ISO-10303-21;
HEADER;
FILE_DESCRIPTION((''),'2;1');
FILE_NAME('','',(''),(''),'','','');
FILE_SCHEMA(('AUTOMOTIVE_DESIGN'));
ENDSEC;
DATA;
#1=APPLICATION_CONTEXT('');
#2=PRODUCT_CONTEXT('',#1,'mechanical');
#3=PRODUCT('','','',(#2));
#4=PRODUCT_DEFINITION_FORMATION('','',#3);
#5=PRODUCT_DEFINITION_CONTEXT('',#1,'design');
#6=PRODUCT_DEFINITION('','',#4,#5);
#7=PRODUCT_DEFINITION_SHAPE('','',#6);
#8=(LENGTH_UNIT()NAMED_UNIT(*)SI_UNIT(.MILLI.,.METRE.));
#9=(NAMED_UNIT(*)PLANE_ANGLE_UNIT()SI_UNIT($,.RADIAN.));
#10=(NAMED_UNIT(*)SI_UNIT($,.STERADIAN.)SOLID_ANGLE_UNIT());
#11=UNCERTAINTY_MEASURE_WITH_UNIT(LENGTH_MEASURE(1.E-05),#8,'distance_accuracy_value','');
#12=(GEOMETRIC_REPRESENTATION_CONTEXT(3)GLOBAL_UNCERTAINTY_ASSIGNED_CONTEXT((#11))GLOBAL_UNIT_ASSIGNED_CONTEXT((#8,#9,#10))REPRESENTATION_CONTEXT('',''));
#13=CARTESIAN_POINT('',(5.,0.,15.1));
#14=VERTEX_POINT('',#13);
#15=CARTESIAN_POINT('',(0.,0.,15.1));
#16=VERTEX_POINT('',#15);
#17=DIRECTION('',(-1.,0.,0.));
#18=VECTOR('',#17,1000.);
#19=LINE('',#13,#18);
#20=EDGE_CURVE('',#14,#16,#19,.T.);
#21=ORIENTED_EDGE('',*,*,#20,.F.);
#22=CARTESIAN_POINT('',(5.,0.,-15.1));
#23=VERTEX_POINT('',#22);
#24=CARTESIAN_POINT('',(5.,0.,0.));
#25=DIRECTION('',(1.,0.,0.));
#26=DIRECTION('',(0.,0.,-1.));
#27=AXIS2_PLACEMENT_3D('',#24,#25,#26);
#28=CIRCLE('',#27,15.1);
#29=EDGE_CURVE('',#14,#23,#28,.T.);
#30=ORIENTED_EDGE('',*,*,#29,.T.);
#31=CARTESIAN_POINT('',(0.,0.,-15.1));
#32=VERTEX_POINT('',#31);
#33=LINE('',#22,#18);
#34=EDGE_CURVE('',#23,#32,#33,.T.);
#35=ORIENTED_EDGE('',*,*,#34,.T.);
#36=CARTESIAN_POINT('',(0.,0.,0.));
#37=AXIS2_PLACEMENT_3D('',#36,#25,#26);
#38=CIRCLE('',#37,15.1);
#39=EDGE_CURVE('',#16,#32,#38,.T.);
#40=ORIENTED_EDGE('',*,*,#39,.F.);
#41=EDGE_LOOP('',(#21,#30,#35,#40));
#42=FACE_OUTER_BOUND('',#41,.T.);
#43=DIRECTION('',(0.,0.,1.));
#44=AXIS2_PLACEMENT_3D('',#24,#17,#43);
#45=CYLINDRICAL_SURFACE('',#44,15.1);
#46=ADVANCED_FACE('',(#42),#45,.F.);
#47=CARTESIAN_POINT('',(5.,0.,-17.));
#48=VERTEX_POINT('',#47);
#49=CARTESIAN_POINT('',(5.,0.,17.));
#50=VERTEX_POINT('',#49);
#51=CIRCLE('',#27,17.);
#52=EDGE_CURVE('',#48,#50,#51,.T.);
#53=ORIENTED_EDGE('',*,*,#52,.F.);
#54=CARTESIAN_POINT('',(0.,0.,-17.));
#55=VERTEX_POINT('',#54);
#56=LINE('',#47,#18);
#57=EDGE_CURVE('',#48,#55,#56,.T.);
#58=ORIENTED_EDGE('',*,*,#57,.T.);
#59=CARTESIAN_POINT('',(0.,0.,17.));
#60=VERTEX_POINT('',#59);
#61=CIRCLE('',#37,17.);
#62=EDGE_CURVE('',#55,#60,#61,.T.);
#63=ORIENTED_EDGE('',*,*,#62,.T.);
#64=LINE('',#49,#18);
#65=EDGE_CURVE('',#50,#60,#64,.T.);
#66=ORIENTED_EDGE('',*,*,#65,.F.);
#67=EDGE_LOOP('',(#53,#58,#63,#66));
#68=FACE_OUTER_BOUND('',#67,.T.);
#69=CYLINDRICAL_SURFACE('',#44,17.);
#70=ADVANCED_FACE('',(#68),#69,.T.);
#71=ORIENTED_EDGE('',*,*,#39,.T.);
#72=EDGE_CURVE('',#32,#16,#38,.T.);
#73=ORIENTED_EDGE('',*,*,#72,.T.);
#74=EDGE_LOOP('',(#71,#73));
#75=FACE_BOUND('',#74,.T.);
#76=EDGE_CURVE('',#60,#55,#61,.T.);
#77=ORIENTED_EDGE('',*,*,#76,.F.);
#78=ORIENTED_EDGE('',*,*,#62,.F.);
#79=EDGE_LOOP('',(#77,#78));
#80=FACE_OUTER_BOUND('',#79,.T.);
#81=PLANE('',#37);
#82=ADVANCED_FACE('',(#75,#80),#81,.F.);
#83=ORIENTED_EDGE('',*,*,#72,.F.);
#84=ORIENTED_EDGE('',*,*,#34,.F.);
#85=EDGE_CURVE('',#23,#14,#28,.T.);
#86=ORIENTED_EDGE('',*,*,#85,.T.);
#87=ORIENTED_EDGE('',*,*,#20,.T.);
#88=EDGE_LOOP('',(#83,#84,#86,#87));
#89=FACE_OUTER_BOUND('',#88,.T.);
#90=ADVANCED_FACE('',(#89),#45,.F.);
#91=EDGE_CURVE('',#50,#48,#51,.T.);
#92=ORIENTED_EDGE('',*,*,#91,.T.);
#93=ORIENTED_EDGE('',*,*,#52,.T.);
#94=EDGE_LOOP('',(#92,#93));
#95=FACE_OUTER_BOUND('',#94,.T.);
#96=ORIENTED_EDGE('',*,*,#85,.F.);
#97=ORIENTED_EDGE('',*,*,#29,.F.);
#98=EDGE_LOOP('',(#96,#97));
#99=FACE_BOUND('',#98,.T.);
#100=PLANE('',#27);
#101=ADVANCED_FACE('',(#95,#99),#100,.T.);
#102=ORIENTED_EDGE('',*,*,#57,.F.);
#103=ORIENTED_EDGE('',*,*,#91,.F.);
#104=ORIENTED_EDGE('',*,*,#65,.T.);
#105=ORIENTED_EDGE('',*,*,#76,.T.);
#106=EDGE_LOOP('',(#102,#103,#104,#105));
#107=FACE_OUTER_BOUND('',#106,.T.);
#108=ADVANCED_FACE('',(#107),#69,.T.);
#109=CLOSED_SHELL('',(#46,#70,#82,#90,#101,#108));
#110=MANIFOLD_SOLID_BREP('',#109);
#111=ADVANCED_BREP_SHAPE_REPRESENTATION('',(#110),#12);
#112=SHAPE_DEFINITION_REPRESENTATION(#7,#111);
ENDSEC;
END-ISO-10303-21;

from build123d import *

# Parameters (mm, degrees)
SKETCH_1_R      = 17
SKETCH_1_R_2    = 15.1
EXTRUDE_1_DEPTH = 5


with BuildPart() as part:
    # 草图1 → 凸台-拉伸1 (new body)
    with BuildSketch(Plane(origin=(0, 0, 0), x_dir=(0, 0, -1), z_dir=(1, 0, 0))):
        Circle(SKETCH_1_R)
        Circle(SKETCH_1_R_2, mode=Mode.SUBTRACT)
    extrude(amount=EXTRUDE_1_DEPTH)


solid = part.part
